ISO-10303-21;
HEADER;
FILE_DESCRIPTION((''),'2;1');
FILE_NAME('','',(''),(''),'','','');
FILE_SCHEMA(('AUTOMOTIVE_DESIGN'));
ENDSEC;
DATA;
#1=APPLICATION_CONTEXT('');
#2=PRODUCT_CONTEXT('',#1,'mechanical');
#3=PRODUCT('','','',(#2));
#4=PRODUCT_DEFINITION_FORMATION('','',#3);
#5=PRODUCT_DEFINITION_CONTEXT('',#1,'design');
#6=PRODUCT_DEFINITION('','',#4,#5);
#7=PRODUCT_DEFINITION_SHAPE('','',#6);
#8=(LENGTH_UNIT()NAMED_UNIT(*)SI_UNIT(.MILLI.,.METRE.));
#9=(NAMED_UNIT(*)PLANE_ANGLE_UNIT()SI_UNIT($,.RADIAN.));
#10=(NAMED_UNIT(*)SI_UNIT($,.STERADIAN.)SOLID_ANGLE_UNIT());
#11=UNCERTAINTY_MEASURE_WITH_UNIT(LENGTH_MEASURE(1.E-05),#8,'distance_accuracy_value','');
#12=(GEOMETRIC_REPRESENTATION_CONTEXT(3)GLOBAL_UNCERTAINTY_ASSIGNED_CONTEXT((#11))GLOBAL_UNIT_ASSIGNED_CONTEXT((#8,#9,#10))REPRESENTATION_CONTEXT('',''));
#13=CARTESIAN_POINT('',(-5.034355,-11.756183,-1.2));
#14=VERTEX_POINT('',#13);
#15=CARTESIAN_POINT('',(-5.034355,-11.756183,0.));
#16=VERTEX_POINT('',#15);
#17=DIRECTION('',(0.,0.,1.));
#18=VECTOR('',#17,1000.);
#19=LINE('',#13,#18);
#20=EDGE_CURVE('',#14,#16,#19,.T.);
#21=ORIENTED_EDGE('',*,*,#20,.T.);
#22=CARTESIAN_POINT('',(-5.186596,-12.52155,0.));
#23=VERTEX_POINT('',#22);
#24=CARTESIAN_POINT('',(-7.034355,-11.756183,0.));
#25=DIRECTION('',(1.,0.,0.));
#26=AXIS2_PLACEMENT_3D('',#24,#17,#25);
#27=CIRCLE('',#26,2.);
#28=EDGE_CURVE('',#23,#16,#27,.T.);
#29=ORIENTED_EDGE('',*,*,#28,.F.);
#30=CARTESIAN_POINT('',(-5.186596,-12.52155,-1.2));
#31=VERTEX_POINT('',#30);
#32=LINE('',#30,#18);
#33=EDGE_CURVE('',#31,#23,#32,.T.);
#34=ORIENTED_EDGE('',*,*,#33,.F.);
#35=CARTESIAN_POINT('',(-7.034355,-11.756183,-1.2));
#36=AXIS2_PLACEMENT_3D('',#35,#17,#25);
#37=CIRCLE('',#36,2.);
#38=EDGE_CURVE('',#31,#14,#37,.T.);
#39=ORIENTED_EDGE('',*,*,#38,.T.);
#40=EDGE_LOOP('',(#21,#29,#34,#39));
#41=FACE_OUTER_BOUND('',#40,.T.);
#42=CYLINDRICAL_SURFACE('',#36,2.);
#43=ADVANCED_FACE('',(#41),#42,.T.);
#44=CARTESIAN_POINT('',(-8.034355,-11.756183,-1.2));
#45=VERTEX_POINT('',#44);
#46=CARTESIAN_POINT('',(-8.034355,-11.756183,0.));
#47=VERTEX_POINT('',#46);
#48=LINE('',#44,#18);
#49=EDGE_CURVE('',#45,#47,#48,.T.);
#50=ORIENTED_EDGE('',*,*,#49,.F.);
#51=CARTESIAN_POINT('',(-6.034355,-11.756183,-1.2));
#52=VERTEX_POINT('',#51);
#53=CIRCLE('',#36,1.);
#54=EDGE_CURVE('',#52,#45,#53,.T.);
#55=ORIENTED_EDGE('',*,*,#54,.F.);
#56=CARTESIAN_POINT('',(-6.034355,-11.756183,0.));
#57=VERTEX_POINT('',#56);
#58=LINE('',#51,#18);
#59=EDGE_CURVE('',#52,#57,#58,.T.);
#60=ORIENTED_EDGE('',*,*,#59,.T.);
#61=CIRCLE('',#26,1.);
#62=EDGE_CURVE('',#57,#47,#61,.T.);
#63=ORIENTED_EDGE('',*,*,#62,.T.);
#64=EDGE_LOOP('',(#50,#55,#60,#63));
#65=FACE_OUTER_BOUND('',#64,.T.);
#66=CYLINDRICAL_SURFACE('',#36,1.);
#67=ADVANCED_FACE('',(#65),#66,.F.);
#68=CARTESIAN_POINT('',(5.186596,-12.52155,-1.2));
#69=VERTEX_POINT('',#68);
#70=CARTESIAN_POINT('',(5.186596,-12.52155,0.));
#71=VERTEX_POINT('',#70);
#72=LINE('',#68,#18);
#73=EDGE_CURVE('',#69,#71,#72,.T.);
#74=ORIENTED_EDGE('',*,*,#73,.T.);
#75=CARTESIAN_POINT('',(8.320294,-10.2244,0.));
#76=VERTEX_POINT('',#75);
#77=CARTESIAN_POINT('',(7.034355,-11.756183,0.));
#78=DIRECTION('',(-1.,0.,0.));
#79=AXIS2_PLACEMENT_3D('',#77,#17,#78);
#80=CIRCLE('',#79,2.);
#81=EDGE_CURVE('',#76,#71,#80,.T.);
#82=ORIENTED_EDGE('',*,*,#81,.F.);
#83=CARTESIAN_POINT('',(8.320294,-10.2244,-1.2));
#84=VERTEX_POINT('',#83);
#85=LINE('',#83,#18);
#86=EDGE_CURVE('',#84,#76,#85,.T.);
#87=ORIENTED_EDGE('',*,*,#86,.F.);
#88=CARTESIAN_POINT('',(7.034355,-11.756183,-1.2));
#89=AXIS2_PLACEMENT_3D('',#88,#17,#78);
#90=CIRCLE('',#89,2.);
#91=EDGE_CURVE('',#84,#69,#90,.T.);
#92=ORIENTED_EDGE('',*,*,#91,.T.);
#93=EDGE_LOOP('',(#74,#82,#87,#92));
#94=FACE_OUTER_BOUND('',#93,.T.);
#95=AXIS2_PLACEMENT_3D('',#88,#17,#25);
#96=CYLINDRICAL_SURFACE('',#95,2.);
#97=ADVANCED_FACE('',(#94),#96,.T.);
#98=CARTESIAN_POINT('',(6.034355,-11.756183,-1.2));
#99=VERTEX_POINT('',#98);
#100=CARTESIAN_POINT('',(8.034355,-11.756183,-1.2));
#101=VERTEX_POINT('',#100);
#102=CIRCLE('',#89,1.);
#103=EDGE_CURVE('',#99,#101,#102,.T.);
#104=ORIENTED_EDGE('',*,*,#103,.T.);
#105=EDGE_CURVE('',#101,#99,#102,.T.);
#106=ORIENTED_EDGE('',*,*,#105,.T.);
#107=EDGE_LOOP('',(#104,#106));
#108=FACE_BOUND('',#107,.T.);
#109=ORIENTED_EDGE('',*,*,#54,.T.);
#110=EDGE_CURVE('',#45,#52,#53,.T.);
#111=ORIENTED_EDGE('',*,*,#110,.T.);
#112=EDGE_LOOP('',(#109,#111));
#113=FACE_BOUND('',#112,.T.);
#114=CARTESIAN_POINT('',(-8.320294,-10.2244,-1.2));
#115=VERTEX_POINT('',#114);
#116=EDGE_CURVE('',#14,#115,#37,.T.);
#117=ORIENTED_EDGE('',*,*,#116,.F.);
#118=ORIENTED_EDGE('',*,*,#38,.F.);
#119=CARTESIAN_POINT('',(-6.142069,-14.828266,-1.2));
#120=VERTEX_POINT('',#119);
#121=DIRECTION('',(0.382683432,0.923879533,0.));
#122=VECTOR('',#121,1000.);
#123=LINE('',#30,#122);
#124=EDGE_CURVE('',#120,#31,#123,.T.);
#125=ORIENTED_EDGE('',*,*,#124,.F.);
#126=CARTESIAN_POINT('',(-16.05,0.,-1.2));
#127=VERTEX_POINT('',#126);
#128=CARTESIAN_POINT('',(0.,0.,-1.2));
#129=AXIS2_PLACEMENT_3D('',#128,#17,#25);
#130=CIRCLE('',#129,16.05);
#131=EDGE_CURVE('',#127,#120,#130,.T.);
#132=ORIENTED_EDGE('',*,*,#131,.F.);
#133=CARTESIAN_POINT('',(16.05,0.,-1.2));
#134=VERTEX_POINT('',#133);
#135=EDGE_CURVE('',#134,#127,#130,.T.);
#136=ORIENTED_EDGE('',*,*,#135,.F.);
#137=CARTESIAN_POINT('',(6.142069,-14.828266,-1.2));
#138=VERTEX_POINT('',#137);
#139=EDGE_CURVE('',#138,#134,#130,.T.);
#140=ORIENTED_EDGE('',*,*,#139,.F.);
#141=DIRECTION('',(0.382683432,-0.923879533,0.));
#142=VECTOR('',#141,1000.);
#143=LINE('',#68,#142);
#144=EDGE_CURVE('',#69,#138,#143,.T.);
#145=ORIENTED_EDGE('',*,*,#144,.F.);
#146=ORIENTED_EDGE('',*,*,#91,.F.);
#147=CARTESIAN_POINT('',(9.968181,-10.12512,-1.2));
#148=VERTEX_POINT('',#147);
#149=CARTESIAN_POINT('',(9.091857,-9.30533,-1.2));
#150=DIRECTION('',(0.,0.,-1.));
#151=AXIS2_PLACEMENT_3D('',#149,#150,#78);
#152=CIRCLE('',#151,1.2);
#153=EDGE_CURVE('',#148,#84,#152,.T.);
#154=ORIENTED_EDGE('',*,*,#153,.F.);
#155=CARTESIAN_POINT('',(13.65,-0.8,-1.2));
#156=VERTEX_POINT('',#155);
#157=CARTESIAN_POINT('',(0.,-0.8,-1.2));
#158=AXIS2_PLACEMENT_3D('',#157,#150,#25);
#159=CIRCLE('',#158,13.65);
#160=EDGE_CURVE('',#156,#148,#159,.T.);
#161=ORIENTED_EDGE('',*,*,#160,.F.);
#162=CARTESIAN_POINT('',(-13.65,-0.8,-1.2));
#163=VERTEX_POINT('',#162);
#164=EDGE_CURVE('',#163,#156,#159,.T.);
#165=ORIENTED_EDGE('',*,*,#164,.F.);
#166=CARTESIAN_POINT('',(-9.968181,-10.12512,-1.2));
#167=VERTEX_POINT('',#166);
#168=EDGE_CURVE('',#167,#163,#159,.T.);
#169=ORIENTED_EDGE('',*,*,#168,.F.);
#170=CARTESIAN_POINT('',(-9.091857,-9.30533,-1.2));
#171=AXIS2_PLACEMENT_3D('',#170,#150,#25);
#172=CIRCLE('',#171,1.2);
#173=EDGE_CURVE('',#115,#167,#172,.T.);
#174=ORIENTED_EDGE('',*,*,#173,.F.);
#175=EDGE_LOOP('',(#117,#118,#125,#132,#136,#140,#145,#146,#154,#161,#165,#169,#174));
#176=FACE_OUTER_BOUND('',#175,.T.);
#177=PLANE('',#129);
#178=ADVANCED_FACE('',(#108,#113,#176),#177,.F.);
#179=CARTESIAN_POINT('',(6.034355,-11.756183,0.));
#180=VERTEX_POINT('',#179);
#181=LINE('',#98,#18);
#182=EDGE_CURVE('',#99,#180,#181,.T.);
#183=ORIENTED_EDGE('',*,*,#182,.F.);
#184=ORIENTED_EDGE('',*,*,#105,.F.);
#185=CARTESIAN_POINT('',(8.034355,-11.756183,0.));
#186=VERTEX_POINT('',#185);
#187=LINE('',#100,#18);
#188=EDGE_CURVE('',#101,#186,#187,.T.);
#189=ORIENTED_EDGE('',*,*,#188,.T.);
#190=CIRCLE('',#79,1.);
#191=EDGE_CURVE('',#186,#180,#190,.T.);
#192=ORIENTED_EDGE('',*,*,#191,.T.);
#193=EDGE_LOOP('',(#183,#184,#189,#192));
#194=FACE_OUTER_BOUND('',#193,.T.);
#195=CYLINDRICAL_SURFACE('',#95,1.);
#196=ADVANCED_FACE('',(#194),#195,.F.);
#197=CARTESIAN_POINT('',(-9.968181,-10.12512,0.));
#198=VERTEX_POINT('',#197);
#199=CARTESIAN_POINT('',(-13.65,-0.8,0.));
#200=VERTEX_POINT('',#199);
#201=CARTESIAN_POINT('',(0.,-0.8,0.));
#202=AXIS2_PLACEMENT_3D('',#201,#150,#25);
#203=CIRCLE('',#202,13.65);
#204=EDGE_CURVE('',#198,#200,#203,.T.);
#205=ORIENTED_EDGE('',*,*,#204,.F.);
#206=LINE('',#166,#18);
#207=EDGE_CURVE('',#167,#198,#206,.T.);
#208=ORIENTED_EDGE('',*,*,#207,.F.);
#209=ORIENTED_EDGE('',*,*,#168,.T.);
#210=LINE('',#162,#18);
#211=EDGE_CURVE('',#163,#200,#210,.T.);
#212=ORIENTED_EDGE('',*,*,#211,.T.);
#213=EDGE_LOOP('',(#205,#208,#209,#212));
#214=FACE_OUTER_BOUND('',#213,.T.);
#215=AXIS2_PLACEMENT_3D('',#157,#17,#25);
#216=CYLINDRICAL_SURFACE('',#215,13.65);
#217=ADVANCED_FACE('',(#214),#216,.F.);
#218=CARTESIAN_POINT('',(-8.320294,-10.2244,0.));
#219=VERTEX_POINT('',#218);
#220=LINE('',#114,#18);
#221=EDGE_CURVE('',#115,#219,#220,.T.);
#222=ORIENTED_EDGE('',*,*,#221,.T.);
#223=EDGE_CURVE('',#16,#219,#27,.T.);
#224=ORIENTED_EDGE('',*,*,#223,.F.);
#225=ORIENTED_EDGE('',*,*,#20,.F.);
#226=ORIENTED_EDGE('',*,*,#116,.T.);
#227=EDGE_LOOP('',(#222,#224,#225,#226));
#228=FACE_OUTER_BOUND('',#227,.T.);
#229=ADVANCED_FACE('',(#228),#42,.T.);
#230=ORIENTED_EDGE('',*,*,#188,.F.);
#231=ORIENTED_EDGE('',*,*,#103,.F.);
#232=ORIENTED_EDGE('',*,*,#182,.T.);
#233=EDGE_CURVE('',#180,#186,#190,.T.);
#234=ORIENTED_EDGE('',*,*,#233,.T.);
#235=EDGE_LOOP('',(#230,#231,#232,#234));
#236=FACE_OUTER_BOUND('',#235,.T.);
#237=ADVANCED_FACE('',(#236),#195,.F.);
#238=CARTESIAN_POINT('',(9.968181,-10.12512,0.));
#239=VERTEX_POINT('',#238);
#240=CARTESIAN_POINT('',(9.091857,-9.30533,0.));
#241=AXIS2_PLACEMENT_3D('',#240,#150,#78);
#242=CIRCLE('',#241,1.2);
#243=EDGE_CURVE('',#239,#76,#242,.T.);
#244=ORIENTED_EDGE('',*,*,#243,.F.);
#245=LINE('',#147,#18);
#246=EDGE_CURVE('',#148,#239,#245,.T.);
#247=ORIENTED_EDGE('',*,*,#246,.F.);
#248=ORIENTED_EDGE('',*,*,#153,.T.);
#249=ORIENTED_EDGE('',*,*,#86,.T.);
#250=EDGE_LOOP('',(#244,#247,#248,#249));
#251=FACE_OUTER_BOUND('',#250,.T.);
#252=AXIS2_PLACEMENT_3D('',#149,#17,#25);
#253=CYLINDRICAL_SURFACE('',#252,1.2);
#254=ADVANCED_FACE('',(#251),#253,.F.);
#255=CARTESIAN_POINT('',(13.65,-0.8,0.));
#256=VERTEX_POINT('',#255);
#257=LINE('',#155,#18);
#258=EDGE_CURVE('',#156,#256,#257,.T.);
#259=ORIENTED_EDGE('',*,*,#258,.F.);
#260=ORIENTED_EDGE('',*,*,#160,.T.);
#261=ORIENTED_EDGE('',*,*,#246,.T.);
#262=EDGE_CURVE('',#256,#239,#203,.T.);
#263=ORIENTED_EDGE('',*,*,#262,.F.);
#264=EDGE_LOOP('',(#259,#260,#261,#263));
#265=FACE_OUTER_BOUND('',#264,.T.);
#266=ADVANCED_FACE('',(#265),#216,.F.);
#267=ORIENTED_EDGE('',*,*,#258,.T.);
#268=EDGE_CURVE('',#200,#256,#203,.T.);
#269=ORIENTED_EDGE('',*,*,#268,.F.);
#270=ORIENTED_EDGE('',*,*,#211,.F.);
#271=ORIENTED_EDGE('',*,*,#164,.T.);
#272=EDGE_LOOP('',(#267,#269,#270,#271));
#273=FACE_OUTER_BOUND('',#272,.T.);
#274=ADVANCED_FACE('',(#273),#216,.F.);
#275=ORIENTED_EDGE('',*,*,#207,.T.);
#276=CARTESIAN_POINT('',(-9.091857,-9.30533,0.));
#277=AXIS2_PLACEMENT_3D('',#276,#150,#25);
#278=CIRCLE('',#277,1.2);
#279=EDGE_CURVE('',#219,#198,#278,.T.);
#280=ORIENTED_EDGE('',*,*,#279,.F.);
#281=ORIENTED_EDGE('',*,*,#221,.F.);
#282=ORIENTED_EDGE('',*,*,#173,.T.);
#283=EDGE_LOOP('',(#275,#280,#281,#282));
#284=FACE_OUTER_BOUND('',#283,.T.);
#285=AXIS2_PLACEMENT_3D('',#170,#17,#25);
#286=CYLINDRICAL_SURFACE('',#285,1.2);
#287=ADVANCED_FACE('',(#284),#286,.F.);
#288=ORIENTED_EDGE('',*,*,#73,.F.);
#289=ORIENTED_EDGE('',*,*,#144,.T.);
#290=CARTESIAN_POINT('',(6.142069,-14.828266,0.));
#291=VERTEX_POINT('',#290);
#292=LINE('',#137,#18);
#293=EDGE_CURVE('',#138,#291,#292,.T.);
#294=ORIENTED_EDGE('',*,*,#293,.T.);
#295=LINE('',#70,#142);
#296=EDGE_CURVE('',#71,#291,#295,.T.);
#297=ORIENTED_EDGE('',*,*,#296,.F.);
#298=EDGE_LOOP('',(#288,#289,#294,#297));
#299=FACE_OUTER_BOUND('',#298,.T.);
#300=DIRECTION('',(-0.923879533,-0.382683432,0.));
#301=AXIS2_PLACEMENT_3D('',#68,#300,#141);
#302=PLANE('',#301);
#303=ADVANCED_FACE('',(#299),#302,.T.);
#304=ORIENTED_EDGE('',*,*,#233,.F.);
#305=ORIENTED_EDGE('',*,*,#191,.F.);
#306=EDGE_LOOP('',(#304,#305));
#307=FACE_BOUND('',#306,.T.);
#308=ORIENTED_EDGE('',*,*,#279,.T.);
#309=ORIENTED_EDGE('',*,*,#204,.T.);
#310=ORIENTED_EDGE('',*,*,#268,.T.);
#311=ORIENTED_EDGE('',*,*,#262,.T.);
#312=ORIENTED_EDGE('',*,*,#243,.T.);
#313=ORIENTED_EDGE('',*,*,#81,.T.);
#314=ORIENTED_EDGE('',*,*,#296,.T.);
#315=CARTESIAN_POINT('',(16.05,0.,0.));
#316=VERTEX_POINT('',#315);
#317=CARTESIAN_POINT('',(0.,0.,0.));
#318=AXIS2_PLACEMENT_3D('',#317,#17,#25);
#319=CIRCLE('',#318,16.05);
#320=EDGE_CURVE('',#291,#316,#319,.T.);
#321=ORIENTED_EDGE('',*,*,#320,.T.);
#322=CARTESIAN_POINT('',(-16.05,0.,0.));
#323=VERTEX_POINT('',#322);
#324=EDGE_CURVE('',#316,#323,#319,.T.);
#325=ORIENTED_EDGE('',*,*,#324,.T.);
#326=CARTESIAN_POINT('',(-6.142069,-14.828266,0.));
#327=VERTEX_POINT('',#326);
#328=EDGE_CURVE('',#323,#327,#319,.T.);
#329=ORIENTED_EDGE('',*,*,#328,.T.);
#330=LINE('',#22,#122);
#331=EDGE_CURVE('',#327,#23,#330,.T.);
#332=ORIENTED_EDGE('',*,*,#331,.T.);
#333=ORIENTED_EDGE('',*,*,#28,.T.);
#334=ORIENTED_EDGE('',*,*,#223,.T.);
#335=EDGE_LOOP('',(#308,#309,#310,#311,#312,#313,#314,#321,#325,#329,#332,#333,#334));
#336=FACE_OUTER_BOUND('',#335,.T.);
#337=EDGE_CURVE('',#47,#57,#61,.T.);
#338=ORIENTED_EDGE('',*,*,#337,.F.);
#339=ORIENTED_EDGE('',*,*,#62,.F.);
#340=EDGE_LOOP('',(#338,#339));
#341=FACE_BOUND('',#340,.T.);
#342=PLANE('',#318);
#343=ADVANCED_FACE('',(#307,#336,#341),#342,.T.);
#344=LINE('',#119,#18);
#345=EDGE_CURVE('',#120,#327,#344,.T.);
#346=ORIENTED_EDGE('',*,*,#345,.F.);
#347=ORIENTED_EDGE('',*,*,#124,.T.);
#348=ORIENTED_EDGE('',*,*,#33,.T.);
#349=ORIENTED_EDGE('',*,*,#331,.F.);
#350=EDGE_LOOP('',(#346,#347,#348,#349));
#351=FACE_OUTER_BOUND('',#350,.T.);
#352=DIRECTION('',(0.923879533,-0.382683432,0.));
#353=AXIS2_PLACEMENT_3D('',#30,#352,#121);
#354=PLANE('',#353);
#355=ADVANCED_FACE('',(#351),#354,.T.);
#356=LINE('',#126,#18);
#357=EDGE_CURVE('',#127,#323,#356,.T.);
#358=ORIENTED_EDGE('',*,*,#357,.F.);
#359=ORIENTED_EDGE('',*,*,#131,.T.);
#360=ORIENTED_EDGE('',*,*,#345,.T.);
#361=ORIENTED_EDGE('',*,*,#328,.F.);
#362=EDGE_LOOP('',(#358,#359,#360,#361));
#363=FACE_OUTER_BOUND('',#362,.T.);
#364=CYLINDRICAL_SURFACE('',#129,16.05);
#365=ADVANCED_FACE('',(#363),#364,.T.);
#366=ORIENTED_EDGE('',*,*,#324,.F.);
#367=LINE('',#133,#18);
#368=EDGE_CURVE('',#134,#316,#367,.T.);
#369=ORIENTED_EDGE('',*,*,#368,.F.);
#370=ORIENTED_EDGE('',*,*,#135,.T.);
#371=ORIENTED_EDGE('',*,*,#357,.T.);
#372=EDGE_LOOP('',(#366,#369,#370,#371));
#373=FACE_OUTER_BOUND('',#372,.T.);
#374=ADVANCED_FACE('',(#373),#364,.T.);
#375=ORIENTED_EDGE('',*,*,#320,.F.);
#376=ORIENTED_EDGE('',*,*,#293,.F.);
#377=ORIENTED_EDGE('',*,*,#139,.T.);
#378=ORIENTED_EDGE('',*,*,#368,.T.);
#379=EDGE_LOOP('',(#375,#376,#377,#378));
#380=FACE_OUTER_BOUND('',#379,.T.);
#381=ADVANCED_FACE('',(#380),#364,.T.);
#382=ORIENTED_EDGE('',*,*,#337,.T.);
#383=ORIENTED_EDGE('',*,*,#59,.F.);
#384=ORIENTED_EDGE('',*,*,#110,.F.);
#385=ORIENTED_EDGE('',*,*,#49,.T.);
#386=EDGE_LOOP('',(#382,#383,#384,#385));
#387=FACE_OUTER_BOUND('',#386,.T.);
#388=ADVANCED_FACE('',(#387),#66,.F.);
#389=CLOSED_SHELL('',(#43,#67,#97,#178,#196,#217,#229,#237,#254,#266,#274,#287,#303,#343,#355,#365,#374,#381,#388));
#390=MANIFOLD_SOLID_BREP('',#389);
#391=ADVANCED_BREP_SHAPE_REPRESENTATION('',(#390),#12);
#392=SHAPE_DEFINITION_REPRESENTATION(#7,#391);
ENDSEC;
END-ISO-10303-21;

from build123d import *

# Parameters (mm, degrees)
SKETCH1_R  = 1
BODY_DEPTH = 1.2


with BuildPart() as part:
    # Sketch1 → Body (new body)
    with BuildSketch(Plane.XY):
        with BuildLine():
            Line((5.186595963, -12.521550316), (6.142069089, -14.828266497))
            ThreePointArc((6.142069089, -14.828266497), (0, 16.05), (-6.142069089, -14.828266497))
            Line((-6.142069089, -14.828266497), (-5.186595963, -12.521550316))
            ThreePointArc((-5.186595963, -12.521550316), (-5.851927185, -10.143153881), (-8.32029392, -10.224399796))
            ThreePointArc((-8.32029392, -10.224399796), (-9.164022184, -10.503157731), (-9.968180846, -10.125120408))
            ThreePointArc((-9.968180846, -10.125120408), (0, 12.85), (9.968180846, -10.125120408))
            ThreePointArc((9.968180846, -10.125120408), (9.164022184, -10.503157731), (8.32029392, -10.224399796))
            ThreePointArc((8.32029392, -10.224399796), (5.851927185, -10.143153881), (5.186595963, -12.521550316))
        make_face()
        with Locations(Location((7.034355028, -11.756183451, 0), (0, 0, 180))):
            Circle(SKETCH1_R, mode=Mode.SUBTRACT)
        with Locations((-7.034355028, -11.756183451)):
            Circle(SKETCH1_R, mode=Mode.SUBTRACT)
    extrude(amount=-BODY_DEPTH)


solid = part.part
